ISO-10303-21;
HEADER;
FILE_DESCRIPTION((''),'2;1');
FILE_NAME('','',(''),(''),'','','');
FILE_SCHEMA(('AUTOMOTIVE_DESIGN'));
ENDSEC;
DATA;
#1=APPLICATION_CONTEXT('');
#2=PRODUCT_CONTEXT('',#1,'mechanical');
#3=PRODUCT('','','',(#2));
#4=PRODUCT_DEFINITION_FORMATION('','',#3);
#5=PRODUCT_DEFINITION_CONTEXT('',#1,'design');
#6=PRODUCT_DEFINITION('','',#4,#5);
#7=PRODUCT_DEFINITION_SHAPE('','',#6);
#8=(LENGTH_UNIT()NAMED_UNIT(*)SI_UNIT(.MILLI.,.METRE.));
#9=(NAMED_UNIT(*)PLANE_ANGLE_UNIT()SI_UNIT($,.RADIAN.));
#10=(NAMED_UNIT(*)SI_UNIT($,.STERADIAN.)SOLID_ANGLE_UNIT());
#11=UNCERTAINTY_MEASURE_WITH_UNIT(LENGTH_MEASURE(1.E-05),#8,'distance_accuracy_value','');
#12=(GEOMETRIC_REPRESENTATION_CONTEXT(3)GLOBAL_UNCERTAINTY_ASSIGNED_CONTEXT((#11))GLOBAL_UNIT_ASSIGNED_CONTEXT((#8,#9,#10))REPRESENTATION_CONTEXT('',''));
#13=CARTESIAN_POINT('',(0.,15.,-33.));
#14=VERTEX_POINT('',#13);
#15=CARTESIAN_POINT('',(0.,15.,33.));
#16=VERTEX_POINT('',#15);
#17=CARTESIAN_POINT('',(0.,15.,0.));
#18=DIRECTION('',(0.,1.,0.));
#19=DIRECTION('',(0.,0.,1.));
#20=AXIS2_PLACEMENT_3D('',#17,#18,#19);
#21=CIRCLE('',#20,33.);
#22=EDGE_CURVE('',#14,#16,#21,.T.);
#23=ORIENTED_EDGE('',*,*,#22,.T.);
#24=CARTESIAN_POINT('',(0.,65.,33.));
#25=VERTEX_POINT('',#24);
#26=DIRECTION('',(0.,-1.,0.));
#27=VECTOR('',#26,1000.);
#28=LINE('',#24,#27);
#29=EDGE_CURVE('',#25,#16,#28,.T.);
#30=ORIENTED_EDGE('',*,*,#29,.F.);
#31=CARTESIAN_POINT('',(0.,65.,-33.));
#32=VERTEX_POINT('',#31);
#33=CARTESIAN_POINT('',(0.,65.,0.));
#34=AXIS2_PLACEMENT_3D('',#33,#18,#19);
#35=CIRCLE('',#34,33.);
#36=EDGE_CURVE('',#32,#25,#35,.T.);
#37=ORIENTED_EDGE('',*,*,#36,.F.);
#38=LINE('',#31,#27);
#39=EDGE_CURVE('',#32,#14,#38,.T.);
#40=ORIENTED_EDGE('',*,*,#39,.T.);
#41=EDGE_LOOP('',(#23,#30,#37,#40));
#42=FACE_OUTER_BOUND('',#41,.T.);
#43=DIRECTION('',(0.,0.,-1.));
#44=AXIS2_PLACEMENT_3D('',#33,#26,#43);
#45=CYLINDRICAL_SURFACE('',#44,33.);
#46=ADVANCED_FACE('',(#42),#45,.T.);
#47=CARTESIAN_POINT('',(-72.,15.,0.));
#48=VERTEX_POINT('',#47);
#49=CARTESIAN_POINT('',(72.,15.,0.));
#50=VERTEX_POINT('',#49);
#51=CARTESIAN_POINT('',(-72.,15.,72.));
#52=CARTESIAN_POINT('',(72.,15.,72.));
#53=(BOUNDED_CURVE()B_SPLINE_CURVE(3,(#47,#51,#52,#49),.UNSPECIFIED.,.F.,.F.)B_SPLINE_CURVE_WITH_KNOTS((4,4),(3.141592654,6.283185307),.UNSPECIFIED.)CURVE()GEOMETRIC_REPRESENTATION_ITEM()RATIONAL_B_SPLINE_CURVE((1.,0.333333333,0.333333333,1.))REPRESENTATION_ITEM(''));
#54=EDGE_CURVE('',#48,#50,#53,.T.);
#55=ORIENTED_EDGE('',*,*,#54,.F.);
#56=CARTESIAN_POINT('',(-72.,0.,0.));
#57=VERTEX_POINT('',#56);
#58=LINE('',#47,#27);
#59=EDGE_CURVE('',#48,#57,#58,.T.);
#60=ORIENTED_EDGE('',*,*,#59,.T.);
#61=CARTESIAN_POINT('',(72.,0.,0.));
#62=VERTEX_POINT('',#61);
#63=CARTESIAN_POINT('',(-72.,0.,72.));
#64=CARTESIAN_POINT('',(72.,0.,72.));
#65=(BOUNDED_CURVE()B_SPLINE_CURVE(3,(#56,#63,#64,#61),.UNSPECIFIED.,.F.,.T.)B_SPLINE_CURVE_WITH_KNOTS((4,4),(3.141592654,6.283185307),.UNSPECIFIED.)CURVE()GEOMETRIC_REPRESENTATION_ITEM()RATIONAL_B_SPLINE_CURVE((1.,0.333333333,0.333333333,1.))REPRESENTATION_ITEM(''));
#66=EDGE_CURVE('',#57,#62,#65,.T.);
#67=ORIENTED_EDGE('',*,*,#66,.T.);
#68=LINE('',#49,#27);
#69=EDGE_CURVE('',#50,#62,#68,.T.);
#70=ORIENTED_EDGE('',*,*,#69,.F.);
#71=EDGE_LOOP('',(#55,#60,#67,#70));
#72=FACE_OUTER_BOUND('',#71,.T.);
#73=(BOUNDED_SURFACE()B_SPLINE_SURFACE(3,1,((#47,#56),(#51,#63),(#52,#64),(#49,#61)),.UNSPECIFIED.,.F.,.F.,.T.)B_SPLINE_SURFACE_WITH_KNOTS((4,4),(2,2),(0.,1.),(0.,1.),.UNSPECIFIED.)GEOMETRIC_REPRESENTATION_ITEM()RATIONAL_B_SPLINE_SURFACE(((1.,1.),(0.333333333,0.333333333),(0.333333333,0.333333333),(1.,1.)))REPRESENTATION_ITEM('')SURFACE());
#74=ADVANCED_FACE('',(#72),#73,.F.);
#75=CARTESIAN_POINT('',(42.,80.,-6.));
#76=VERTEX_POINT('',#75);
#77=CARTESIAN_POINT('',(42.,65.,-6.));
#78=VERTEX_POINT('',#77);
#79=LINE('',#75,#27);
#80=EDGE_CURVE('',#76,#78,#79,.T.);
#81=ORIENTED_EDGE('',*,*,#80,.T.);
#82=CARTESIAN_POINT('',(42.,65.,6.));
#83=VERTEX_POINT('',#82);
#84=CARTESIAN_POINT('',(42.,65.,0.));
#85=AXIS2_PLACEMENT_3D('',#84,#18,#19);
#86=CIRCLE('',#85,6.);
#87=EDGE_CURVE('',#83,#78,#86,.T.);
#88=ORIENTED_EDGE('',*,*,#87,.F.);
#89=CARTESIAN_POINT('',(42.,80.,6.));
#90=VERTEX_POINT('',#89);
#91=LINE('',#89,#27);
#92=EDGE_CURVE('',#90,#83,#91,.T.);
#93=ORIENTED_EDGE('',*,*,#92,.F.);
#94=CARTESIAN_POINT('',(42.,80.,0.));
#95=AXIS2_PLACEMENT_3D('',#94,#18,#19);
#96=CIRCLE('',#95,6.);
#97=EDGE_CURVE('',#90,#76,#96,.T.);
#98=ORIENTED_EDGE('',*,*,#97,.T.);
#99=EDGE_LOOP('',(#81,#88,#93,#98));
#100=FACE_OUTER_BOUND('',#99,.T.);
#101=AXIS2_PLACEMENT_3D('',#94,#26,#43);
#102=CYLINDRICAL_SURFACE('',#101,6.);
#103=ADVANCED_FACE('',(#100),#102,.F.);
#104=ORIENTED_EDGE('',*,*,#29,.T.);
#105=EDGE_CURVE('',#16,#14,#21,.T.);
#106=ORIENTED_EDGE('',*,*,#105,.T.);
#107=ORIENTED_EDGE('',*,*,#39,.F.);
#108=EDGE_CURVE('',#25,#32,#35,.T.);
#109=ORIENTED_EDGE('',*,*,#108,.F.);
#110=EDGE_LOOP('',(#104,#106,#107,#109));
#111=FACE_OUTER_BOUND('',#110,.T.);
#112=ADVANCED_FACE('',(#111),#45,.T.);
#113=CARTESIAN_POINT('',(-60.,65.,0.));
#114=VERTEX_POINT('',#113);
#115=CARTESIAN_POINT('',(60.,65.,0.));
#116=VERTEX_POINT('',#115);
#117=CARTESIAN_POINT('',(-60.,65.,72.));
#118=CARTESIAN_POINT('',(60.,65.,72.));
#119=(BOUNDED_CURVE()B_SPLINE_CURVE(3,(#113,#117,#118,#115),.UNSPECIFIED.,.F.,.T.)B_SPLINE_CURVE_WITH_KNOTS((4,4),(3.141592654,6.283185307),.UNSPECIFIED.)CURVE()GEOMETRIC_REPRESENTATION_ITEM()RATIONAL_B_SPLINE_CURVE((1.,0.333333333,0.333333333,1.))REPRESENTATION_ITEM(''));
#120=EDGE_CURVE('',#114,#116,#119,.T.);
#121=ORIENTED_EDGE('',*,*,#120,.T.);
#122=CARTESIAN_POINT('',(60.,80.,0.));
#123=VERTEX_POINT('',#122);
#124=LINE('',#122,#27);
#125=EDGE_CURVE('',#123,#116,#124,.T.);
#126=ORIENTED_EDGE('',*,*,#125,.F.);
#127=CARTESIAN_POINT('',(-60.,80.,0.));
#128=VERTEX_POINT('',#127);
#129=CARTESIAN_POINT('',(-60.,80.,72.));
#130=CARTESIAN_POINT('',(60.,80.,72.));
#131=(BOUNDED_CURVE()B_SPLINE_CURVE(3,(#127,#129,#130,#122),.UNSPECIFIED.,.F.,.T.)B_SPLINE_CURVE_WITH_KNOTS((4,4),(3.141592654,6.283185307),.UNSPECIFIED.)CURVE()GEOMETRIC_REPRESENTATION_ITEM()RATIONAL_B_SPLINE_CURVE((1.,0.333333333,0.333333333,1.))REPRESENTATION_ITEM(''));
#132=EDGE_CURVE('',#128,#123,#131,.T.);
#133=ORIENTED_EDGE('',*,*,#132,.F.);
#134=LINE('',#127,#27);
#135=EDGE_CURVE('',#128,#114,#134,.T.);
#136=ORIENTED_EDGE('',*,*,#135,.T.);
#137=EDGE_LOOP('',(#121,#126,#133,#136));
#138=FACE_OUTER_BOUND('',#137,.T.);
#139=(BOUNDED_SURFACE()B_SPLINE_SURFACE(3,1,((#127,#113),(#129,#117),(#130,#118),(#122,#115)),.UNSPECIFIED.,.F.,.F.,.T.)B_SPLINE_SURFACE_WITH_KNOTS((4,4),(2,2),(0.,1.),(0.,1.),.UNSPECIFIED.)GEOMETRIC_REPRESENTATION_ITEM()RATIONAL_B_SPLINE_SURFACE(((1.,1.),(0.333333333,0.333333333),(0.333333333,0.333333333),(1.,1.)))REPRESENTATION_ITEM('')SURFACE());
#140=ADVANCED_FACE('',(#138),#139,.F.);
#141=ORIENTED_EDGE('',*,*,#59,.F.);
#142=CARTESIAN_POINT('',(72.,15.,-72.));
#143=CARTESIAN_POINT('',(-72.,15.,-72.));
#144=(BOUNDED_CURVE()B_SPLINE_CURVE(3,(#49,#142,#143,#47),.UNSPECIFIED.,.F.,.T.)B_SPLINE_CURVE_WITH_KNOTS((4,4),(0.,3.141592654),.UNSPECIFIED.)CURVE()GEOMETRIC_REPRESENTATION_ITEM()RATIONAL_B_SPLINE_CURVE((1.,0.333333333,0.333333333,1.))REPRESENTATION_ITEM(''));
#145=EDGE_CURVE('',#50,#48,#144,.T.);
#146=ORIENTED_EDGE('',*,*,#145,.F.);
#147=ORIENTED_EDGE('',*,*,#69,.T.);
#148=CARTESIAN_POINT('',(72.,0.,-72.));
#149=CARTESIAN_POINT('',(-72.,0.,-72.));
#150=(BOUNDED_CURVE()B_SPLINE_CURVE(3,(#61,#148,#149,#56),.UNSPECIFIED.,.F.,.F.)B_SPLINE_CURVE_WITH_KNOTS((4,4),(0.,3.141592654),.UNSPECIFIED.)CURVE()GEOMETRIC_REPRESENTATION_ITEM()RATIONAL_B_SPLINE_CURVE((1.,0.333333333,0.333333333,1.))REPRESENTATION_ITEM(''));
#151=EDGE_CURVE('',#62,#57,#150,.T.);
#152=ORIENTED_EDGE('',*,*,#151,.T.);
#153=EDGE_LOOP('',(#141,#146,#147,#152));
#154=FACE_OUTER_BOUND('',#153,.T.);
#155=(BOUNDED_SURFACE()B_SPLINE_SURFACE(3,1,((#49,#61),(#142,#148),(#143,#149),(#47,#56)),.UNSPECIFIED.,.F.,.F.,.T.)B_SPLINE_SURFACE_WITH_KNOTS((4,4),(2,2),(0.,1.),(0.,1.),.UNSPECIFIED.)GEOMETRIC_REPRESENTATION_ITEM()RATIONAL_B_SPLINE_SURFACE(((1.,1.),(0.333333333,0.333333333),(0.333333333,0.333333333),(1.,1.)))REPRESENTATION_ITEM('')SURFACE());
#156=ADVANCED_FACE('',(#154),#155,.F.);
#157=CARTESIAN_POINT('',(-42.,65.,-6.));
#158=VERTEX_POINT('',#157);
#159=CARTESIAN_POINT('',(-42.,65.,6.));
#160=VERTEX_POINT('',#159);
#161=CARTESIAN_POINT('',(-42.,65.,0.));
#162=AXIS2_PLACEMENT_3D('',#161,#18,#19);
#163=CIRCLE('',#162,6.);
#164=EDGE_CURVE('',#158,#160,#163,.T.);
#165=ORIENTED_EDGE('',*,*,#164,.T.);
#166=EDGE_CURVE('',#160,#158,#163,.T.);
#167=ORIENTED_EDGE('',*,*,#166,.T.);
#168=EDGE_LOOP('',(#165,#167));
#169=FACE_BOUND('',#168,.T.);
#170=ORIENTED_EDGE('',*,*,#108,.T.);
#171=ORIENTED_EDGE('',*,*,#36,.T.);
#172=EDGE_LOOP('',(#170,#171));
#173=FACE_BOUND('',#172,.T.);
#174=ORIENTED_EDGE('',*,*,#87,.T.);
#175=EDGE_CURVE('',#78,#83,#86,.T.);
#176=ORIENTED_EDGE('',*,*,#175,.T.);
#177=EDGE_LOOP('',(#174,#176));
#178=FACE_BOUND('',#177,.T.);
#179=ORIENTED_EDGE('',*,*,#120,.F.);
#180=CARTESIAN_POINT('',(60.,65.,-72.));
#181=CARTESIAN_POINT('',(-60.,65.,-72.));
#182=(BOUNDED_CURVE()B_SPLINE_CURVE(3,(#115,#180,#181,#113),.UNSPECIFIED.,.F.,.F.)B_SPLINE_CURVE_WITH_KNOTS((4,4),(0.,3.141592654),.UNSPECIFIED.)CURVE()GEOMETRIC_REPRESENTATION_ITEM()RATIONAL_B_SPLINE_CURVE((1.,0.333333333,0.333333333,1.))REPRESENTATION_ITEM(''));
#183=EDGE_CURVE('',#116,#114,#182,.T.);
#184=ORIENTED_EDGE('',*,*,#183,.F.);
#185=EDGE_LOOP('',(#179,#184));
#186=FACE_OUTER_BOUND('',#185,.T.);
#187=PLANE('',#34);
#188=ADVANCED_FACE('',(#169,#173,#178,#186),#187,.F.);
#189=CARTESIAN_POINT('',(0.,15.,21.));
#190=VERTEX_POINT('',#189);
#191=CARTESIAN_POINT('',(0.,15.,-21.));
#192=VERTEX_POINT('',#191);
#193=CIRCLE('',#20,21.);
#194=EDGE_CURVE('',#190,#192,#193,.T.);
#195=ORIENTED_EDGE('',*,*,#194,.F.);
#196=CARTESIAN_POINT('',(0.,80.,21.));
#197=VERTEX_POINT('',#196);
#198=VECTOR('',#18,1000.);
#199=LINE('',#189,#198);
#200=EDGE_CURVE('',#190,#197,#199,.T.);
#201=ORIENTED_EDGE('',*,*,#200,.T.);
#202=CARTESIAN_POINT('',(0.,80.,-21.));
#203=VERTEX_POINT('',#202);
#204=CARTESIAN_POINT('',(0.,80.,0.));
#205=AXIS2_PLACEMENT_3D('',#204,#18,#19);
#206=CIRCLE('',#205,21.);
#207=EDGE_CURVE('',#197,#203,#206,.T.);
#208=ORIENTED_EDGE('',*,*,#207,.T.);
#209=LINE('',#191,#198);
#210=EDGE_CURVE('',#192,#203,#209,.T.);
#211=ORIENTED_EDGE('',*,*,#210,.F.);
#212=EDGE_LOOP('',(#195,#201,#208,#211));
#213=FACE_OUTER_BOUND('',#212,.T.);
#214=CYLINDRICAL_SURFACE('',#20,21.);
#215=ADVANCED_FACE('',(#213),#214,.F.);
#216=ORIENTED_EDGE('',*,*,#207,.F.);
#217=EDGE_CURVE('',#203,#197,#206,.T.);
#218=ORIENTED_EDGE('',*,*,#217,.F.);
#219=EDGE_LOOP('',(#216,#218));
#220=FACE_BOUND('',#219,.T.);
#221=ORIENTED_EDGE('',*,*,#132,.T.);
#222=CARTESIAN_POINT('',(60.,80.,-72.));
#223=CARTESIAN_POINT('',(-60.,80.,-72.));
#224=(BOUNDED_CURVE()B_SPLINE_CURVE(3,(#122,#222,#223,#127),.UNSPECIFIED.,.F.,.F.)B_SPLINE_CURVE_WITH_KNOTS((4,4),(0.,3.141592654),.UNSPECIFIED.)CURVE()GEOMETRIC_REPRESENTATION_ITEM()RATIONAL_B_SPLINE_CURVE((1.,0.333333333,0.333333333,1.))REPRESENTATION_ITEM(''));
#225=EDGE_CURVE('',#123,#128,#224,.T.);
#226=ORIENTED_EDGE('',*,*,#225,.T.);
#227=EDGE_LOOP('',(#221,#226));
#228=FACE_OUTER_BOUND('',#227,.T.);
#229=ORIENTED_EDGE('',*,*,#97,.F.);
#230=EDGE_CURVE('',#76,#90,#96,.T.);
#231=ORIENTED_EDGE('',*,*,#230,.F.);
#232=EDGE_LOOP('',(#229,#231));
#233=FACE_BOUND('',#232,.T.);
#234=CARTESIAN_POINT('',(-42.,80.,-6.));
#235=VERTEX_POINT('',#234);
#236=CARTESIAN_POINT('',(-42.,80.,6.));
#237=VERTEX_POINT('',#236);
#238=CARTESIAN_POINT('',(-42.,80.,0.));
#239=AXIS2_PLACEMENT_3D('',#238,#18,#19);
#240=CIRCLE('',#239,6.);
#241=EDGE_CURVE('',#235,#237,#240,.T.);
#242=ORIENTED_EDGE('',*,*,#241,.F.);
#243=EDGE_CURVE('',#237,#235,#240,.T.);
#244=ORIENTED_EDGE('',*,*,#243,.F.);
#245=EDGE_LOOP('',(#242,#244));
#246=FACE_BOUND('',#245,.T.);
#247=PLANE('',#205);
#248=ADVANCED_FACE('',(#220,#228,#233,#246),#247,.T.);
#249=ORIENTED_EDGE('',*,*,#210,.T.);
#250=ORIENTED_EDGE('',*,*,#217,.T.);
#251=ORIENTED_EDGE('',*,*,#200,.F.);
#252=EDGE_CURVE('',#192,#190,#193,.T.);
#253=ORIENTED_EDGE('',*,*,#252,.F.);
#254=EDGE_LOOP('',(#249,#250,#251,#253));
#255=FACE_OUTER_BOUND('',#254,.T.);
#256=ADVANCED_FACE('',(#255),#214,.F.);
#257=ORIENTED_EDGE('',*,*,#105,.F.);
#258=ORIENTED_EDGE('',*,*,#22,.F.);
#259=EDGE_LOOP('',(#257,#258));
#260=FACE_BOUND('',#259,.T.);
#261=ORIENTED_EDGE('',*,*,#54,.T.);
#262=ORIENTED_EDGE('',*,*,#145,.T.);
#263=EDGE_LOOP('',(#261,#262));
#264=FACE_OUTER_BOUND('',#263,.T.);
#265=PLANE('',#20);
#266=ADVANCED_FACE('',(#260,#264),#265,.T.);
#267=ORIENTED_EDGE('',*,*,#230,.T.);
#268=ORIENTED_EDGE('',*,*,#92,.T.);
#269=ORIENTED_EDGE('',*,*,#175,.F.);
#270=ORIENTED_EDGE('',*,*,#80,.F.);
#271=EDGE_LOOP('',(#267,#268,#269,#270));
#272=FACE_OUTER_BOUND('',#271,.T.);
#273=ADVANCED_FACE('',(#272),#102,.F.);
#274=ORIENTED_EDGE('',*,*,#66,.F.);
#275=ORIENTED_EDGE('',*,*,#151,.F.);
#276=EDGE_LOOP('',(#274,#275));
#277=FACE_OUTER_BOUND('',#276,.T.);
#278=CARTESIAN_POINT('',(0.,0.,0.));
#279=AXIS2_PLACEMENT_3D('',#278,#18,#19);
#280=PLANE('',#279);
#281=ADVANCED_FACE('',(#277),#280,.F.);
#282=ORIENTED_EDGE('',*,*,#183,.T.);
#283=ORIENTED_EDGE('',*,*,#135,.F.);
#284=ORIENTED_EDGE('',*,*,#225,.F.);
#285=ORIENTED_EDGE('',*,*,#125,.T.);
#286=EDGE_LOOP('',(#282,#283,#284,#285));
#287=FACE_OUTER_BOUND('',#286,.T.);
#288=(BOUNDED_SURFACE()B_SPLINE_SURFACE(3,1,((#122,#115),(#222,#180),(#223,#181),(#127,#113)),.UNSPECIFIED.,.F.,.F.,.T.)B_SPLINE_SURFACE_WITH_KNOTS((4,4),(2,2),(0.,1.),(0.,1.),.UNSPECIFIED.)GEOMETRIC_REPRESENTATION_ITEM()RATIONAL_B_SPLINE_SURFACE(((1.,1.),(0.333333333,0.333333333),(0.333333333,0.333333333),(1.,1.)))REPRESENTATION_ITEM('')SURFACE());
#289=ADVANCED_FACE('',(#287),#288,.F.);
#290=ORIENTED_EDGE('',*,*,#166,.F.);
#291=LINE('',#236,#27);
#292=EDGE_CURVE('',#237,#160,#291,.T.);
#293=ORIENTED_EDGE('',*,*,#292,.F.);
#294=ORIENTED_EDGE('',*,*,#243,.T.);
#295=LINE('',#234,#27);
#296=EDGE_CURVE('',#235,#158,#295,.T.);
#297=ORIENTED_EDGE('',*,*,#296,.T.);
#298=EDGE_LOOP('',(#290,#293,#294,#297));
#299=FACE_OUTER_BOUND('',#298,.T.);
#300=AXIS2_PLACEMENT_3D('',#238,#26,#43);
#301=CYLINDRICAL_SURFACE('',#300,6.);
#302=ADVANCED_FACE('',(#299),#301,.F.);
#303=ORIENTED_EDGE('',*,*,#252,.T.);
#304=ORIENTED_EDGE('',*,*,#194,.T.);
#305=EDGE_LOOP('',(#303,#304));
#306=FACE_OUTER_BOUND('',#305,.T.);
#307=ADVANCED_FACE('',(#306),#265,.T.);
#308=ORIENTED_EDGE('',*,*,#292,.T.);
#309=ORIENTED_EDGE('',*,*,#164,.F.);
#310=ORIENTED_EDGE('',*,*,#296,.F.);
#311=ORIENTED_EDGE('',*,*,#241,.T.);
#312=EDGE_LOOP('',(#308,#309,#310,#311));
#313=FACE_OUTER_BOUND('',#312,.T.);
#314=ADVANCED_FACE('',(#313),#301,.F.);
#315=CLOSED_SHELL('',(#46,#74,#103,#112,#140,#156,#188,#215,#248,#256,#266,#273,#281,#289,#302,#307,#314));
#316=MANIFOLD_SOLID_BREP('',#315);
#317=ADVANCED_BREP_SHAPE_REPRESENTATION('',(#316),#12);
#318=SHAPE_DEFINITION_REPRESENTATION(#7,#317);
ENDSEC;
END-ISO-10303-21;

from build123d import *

# Parameters (mm, degrees)
BASE_FLANGE_SKETCH_RX             = 72
BASE_FLANGE_SKETCH_RY             = 36
BASE_FLANGE_DEPTH                 = 15
CENTER_BOSS_SKETCH_R              = 33
CENTER_BOSS_66_DEPTH              = 50
TOP_FLANGE_SKETCH_RX              = 60
TOP_FLANGE_SKETCH_RY              = 36
TOP_FLANGE_SKETCH_R               = 6
TOP_FLANGE_WITH_HOLES_2X_12_DEPTH = 15
BORE_SKETCH_R                     = 21
BORE_42_DEPTH                     = 65


with BuildPart() as part:
    # Base Flange Sketch → Base Flange (new body)
    with BuildSketch(Plane(origin=(0, 0, 0), x_dir=(1, 0, 0), z_dir=(0, 1, 0))):
        with Locations((0, 0)):
            Ellipse(BASE_FLANGE_SKETCH_RX, BASE_FLANGE_SKETCH_RY)
    extrude(amount=BASE_FLANGE_DEPTH)

    # Center Boss Sketch → Center Boss Ø66 (add)
    with BuildSketch(Plane(origin=(0, 15, 0), x_dir=(1, 0, 0), z_dir=(0, 1, 0))):
        with Locations(Location((0, 0, 0), (0, 0, 270))):
            Circle(CENTER_BOSS_SKETCH_R)
    extrude(amount=CENTER_BOSS_66_DEPTH)

    # Top Flange Sketch → Top Flange with Holes 2xØ12 (add)
    with BuildSketch(Plane(origin=(0, 65, 0), x_dir=(1, 0, 0), z_dir=(0, 1, 0))):
        with Locations((0, 0)):
            Ellipse(TOP_FLANGE_SKETCH_RX, TOP_FLANGE_SKETCH_RY)
        with Locations(Location((-42, 0, 0), (0, 0, 270))):
            Circle(TOP_FLANGE_SKETCH_R, mode=Mode.SUBTRACT)
        with Locations(Location((42, 0, 0), (0, 0, 270))):
            Circle(TOP_FLANGE_SKETCH_R, mode=Mode.SUBTRACT)
    extrude(amount=TOP_FLANGE_WITH_HOLES_2X_12_DEPTH)

    # Bore Sketch → Bore Ø42 (cut)
    with BuildSketch(Plane(origin=(0, 80, 0), x_dir=(1, 0, 0), z_dir=(0, 1, 0))):
        with Locations(Location((0, 0, 0), (0, 0, 270))):
            Circle(BORE_SKETCH_R)
    extrude(amount=-BORE_42_DEPTH, mode=Mode.SUBTRACT)


solid = part.part
